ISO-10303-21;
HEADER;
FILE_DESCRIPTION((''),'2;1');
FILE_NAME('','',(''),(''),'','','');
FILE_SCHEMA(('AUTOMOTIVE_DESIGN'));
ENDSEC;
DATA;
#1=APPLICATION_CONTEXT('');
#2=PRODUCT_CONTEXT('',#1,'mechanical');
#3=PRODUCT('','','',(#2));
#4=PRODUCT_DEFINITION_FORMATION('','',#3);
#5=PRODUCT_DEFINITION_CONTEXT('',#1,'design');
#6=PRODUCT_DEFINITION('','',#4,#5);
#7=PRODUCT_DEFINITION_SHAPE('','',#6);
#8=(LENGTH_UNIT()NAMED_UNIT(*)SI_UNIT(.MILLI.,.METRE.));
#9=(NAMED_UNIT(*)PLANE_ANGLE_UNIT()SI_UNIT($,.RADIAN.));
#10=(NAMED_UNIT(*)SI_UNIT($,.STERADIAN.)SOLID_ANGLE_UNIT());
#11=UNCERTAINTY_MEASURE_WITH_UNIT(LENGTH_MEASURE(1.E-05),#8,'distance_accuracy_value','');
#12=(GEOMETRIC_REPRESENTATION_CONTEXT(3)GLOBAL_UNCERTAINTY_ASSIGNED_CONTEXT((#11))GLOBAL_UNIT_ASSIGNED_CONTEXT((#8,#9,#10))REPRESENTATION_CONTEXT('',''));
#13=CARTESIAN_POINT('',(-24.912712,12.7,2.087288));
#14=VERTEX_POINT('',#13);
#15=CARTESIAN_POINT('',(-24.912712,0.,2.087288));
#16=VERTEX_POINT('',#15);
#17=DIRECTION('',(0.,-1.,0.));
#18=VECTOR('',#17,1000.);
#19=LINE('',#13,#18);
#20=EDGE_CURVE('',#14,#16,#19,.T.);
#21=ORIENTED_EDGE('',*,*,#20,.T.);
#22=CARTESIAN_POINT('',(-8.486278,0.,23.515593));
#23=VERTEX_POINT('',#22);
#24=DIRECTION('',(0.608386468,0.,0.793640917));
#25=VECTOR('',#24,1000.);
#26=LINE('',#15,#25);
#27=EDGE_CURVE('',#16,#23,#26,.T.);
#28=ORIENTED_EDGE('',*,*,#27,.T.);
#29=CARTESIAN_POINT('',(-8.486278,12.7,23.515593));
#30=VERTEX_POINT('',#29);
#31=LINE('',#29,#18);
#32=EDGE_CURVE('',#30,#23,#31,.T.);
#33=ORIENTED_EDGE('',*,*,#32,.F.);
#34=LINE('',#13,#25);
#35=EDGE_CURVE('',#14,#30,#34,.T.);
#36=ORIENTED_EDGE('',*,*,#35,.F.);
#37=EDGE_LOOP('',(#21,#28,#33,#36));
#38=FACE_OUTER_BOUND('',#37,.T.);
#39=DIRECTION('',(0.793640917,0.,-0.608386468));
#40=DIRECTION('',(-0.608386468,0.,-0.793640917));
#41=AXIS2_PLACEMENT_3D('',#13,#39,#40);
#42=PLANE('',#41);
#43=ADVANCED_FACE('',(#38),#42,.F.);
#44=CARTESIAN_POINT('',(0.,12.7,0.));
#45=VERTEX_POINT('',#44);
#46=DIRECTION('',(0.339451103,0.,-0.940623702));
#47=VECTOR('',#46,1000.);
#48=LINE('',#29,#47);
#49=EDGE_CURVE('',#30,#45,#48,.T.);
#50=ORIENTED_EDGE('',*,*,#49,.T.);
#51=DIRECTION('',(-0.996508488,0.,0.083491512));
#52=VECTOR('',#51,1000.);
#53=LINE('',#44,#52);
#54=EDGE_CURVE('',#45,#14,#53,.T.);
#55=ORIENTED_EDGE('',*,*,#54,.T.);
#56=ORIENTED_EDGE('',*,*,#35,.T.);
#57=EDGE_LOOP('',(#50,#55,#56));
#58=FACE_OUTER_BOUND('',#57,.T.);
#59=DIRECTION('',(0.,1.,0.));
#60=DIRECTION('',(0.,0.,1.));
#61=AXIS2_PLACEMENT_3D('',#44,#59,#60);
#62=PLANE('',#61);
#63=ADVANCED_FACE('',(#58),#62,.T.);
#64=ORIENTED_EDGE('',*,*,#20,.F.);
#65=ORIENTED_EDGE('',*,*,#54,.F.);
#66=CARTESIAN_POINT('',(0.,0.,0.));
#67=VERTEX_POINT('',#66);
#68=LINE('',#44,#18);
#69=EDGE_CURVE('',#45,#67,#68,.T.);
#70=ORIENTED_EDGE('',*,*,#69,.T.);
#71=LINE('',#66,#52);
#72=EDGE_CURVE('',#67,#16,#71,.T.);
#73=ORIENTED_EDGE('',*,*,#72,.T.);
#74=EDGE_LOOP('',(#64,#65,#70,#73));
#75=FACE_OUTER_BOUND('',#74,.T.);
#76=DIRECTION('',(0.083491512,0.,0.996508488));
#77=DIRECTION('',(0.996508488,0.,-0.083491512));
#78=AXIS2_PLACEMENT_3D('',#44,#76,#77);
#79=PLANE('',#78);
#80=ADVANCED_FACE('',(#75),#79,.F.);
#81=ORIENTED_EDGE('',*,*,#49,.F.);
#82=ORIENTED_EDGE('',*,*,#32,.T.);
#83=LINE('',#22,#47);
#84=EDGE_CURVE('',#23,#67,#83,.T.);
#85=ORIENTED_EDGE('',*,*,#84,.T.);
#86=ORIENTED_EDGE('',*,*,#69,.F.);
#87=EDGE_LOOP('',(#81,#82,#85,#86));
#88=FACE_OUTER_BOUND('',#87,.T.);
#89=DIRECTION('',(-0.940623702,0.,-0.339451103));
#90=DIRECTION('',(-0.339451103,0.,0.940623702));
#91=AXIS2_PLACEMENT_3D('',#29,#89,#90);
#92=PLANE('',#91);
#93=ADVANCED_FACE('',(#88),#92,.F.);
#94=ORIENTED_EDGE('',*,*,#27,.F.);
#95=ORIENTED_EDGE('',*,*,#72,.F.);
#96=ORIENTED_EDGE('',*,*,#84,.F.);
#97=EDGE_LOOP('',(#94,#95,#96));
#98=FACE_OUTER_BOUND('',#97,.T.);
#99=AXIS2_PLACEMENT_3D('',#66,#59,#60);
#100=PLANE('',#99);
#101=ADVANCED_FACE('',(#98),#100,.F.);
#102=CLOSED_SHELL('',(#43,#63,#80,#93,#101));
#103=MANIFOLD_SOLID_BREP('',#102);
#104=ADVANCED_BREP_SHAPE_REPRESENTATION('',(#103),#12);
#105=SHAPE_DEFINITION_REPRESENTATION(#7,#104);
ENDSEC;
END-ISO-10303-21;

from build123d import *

# Parameters (mm, degrees)
BOSS_EXTRUDE1_DEPTH = 12.7


with BuildPart() as part:
    # Sketch1 → Boss-Extrude1 (new body)
    with BuildSketch(Plane(origin=(0, 0, 0), x_dir=(1, 0, 0), z_dir=(0, 1, 0))):
        Polygon((0, 0), (-24.912712211, -2.087287789), (-8.486277569, -23.515592551), align=None)
    extrude(amount=BOSS_EXTRUDE1_DEPTH)


solid = part.part
